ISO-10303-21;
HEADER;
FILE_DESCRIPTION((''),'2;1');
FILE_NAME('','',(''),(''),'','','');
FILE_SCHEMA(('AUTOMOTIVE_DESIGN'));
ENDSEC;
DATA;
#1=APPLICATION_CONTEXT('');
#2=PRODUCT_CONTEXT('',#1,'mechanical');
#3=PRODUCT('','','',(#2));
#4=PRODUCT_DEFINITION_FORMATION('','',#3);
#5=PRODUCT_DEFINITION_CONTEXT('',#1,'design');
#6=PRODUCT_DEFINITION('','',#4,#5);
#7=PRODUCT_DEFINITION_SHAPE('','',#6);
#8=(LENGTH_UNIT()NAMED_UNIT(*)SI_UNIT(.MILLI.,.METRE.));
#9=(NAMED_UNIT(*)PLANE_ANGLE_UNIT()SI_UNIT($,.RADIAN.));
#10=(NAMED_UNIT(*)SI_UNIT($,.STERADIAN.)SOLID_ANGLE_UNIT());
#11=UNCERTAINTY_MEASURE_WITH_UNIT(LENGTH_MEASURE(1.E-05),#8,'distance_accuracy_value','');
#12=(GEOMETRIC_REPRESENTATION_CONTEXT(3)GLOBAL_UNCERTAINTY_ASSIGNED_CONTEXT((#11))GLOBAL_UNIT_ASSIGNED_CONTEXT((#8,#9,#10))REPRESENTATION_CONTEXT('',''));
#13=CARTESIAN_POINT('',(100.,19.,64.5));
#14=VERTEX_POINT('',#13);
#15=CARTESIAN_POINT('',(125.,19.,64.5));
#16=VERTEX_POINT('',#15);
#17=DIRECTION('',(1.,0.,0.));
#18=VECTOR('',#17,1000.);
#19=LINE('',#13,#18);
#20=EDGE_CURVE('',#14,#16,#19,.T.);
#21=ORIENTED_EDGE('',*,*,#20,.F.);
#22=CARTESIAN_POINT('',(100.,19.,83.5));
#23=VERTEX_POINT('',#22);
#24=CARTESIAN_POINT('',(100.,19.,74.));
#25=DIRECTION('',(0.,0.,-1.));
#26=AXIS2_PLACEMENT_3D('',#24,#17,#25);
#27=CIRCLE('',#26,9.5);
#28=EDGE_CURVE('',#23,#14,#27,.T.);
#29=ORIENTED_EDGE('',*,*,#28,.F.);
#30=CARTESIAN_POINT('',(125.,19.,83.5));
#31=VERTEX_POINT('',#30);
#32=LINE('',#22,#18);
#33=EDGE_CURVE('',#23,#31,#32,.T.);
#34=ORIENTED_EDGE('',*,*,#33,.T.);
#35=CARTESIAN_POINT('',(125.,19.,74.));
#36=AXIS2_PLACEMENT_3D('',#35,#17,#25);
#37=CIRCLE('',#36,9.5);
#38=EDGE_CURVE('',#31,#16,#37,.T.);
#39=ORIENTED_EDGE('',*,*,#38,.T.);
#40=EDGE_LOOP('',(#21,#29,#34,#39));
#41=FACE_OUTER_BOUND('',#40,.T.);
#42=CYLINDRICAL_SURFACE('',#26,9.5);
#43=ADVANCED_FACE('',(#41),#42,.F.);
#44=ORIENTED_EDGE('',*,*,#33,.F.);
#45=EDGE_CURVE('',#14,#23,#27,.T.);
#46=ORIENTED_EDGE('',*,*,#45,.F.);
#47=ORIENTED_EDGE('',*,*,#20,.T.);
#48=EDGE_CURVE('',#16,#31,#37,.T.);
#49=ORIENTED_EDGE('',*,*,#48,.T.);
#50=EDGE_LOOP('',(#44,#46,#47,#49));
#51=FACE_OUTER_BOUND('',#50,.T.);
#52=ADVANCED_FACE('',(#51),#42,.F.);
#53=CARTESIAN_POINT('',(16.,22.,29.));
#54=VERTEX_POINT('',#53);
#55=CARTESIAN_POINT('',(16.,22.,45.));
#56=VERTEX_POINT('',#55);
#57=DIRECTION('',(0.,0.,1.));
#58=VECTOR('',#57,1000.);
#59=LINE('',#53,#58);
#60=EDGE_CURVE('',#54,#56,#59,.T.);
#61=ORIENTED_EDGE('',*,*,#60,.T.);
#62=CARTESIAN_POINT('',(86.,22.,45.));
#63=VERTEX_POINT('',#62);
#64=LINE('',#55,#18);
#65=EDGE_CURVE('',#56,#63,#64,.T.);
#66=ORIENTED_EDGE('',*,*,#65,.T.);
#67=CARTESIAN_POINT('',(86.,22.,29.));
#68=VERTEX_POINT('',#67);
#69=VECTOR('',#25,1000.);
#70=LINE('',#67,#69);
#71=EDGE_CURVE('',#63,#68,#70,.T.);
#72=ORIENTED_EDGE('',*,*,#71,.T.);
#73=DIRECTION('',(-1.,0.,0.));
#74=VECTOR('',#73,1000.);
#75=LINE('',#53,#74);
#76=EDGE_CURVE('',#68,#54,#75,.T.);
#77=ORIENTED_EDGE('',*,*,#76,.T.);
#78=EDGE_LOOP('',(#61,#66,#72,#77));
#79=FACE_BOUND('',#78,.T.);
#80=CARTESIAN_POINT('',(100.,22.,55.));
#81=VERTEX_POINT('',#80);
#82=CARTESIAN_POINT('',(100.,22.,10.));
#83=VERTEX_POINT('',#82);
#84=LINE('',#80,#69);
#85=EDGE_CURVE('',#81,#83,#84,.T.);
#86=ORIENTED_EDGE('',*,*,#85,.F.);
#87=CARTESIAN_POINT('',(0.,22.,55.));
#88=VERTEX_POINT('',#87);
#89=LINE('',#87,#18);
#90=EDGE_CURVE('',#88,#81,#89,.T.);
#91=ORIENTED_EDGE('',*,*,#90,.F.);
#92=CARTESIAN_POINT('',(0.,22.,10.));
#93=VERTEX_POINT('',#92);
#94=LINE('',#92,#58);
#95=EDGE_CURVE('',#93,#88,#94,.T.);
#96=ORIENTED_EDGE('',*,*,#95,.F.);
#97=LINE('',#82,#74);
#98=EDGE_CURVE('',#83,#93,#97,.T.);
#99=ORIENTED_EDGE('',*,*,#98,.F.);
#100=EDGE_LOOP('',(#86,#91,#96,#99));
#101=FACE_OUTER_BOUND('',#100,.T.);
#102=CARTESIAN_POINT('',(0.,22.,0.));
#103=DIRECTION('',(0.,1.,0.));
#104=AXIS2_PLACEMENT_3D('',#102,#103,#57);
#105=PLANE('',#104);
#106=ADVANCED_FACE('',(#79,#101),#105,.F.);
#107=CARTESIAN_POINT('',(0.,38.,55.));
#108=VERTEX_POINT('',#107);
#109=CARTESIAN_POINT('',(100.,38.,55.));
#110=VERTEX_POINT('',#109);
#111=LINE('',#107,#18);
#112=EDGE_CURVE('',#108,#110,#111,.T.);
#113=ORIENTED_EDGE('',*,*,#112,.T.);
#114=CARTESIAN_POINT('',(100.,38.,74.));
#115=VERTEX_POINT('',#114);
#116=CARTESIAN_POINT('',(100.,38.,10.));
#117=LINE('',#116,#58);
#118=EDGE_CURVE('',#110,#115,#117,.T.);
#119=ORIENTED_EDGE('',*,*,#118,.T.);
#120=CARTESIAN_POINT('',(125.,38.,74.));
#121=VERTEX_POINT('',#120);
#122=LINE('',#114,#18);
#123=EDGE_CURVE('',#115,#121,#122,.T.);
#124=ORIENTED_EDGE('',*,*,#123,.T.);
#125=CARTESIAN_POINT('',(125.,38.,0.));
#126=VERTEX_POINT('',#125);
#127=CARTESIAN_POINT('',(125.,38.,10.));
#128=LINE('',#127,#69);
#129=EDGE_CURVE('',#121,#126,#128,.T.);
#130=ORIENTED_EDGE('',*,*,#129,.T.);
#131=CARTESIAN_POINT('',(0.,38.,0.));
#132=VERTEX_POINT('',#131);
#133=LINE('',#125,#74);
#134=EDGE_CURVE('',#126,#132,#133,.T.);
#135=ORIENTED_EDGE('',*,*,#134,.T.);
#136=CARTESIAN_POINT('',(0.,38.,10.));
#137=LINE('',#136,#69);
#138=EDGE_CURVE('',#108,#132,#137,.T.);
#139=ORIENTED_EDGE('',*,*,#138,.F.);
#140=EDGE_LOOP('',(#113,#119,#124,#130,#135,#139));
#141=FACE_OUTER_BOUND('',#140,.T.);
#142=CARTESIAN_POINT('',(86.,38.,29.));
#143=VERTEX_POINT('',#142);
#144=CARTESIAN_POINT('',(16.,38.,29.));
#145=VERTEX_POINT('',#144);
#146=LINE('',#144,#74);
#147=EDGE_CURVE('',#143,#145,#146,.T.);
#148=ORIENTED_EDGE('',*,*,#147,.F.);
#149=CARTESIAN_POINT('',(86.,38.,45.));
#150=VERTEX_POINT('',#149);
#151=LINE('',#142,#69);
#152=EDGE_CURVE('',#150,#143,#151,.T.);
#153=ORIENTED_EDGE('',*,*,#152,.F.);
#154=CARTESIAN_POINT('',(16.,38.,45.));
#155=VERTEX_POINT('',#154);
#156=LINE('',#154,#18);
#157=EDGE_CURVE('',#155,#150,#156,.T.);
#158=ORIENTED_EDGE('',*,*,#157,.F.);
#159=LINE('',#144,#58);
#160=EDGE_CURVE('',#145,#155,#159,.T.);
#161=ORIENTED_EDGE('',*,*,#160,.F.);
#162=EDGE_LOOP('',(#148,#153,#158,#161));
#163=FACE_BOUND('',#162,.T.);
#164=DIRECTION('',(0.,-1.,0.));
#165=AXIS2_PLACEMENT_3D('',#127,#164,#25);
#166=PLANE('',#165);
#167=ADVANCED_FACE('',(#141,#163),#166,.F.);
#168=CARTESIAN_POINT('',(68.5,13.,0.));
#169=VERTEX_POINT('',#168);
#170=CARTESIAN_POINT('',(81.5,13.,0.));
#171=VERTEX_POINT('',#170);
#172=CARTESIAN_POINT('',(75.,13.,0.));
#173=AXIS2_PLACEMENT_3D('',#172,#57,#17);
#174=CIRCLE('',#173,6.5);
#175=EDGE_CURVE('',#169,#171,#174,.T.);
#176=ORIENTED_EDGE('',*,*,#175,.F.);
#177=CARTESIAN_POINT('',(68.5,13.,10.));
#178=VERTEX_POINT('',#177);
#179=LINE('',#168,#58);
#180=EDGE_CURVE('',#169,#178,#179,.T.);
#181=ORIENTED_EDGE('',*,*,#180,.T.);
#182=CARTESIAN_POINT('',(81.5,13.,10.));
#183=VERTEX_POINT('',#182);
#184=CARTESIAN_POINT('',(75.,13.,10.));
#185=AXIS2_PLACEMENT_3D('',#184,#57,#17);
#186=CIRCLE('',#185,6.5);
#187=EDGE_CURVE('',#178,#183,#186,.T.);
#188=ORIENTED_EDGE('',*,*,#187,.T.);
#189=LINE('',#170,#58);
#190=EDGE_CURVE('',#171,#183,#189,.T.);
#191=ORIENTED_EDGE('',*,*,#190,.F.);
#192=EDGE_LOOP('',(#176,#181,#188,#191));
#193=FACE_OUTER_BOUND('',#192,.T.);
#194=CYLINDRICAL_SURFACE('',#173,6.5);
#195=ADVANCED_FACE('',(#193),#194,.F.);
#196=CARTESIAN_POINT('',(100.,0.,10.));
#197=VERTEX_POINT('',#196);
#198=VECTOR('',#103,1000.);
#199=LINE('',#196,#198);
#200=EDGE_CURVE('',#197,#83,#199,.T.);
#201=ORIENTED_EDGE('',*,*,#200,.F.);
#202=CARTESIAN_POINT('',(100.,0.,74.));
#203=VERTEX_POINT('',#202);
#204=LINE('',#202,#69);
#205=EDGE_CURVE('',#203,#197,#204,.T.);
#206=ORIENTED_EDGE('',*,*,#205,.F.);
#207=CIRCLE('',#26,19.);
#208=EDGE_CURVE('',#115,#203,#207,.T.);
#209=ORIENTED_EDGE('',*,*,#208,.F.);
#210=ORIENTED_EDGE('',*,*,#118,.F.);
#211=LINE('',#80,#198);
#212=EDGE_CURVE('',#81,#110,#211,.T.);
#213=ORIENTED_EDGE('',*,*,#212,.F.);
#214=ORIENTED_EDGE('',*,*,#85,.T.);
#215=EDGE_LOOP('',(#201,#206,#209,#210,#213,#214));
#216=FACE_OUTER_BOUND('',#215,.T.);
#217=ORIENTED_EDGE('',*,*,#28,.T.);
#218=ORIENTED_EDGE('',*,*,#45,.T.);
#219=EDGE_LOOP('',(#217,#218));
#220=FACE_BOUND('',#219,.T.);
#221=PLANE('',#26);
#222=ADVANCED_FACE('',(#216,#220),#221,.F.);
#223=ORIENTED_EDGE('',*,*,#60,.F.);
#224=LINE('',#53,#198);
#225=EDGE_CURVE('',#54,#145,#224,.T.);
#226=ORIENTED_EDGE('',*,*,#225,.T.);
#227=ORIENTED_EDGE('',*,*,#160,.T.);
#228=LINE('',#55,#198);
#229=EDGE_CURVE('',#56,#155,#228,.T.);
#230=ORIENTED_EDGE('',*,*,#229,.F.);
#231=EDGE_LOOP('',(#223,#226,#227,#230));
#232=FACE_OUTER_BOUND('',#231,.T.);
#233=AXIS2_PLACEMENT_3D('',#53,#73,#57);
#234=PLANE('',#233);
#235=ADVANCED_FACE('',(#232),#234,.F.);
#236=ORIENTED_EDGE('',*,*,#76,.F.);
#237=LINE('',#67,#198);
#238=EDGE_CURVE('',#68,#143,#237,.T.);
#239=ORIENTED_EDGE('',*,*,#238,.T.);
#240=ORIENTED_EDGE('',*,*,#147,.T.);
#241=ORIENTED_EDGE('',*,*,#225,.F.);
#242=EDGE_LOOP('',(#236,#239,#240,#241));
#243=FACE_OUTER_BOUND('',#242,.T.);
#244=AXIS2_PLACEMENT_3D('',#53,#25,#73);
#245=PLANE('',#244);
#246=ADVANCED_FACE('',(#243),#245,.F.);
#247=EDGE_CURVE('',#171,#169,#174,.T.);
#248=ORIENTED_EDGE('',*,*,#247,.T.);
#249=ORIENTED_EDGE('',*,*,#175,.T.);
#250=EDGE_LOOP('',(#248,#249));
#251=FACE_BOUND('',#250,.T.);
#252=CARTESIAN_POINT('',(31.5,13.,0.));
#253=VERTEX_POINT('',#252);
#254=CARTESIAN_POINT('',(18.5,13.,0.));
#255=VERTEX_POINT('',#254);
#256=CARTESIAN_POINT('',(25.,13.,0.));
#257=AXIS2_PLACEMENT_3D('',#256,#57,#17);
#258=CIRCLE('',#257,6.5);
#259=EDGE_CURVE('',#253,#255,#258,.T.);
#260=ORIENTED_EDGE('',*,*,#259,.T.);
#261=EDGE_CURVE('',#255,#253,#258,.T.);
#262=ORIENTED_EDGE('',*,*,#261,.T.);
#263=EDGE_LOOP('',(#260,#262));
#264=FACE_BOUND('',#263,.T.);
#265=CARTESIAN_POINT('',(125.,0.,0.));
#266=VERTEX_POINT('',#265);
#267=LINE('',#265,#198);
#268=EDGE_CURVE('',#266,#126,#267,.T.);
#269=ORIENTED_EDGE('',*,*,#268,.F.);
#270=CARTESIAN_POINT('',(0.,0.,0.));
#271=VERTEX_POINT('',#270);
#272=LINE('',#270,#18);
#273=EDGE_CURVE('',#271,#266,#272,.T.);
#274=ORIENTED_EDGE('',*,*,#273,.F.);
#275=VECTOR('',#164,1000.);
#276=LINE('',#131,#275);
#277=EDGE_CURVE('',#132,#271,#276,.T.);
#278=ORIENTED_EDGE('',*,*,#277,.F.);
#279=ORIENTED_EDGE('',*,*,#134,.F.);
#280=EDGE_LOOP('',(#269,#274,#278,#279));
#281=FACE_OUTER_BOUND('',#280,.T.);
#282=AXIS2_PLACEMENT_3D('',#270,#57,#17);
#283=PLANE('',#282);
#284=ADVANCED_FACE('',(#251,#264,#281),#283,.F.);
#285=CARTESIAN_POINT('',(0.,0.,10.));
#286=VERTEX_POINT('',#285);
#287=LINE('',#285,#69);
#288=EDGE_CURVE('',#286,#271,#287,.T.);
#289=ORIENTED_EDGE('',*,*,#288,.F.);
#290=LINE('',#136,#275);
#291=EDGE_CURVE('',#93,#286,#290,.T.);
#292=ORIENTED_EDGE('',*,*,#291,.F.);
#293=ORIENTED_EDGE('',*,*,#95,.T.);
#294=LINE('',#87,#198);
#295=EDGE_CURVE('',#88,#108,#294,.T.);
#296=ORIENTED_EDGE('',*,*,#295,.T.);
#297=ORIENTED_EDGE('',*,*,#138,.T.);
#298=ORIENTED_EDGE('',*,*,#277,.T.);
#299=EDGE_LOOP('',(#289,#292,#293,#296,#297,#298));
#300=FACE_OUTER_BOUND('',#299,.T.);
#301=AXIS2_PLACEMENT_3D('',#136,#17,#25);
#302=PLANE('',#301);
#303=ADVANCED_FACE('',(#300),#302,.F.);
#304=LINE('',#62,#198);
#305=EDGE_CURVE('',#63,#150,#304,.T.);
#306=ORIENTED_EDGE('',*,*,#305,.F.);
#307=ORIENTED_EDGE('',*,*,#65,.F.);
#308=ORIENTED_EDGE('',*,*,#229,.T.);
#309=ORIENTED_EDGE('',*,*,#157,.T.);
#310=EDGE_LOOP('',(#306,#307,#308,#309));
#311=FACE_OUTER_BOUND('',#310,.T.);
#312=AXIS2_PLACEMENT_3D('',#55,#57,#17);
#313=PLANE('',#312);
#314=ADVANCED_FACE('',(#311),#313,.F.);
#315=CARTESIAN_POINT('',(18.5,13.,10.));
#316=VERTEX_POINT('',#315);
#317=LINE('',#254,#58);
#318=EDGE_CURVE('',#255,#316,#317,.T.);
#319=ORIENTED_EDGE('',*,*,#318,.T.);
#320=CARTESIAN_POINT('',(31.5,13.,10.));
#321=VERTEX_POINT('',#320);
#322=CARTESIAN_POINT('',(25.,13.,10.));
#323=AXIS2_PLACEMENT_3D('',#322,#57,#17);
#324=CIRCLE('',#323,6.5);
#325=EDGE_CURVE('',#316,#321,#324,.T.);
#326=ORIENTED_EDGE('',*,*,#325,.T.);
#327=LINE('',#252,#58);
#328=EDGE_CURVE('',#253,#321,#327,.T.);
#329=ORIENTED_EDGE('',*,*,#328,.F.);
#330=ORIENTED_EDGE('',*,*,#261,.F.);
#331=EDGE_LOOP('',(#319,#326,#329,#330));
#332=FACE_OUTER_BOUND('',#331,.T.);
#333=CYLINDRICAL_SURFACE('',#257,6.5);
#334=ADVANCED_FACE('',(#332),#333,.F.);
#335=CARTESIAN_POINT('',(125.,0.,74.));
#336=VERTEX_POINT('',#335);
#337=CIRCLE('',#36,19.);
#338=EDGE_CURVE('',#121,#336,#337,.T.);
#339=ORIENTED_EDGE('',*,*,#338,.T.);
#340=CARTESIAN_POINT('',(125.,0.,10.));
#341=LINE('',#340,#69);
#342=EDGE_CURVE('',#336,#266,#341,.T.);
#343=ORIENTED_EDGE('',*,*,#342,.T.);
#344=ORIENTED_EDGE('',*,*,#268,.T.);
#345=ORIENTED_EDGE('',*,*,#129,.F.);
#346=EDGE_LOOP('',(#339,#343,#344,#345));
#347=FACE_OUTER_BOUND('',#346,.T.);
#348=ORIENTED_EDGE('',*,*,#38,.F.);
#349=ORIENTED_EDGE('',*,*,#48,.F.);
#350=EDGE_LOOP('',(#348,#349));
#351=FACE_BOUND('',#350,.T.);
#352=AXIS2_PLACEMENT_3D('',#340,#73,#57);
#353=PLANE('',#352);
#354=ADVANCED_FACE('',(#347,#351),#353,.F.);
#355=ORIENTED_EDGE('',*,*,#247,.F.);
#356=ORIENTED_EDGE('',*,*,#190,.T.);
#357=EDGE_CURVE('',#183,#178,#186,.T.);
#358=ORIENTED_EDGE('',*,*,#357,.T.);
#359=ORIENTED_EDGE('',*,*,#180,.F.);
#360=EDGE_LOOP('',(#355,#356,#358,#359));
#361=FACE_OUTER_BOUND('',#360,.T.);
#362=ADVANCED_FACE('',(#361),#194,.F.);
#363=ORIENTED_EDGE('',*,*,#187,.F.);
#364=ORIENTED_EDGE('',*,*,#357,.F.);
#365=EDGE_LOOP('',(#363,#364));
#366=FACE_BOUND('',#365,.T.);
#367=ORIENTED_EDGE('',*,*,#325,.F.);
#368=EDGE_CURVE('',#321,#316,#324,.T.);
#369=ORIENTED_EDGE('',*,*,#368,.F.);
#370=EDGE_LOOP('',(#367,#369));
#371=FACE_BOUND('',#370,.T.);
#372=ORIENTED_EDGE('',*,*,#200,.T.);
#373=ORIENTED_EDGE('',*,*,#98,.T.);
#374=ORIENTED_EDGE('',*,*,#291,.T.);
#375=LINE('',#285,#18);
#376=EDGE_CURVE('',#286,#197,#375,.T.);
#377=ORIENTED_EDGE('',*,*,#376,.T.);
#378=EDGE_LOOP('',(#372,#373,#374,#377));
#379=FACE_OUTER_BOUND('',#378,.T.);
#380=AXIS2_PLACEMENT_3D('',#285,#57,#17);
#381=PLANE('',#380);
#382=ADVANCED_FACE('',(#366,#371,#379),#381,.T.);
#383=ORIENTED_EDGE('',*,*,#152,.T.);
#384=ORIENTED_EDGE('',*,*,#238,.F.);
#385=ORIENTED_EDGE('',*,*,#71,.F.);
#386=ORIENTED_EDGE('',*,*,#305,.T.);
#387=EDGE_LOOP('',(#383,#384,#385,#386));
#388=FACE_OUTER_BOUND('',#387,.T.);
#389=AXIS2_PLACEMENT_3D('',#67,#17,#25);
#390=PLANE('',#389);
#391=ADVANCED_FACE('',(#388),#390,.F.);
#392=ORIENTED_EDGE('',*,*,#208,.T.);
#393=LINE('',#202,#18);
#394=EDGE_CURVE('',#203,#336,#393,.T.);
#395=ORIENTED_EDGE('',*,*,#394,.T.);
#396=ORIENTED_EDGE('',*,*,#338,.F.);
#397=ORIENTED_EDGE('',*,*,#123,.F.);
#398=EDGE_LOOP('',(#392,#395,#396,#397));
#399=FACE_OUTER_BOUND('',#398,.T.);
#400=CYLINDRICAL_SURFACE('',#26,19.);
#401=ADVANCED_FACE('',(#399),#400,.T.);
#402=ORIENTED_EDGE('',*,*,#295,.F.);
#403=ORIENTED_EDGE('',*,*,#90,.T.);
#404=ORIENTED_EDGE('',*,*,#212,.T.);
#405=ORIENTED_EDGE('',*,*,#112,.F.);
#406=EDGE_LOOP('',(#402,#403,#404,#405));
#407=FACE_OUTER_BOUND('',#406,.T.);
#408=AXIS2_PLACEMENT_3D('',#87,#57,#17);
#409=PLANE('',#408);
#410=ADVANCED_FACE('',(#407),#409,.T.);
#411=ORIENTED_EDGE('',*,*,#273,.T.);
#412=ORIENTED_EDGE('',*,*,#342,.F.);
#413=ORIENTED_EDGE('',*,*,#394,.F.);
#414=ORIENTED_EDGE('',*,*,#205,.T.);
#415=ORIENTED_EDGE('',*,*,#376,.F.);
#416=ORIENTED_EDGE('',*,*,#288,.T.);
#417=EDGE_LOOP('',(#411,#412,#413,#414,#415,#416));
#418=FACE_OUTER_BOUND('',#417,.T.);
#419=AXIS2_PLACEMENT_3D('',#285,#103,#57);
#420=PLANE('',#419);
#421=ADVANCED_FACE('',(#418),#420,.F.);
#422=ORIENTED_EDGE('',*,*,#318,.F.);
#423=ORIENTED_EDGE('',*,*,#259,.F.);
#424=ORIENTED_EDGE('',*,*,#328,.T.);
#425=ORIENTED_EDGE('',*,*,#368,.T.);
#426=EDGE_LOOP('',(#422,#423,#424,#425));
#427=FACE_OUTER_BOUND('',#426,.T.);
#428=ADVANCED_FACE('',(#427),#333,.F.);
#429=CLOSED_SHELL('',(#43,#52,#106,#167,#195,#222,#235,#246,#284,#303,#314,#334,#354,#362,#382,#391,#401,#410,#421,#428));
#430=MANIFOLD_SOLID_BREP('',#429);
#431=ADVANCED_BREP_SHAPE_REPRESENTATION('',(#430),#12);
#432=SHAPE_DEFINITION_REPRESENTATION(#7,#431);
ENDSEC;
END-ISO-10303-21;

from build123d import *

# Parameters (mm, degrees)
BASE_PLATE_SKETCH_W   = 125
BASE_PLATE_SKETCH_H   = 38
BASE_PLATE_DEPTH      = 10
HINGE_LUG_DEPTH       = 25
LUG_BORE_19_SKETCH_R  = 9.5
LUG_BORE_19_DEPTH     = 25
ARM_SKETCH_W          = 100
ARM_SKETCH_H          = 45
ARM_DEPTH             = 16
SLOT_70X16_SKETCH_W   = 70
SLOT_70X16_SKETCH_H   = 16
SLOT_70X16_DEPTH      = 16
CORNER_NOTCH_SKETCH_R = 6.5
CORNER_NOTCH_DEPTH    = 10


with BuildPart() as part:
    # Base Plate Sketch → Base Plate (new body)
    with BuildSketch(Plane.XY):
        with Locations((62.5, 19)):
            Rectangle(BASE_PLATE_SKETCH_W, BASE_PLATE_SKETCH_H)
    extrude(amount=BASE_PLATE_DEPTH)

    # Hinge Lug Sketch → Hinge Lug (add)
    with BuildSketch(Plane(origin=(125, 0, 0), x_dir=(0, 0, -1), z_dir=(1, 0, 0))):
        with BuildLine():
            Line((-10, 38), (-74, 38))
            ThreePointArc((-74, 38), (-93, 19), (-74, 0))
            Line((-74, 0), (-10, 0))
            Line((-10, 0), (-10, 38))
        make_face()
    extrude(amount=-HINGE_LUG_DEPTH)

    # Lug Bore Ø19 Sketch → Lug Bore Ø19 (cut)
    with BuildSketch(Plane(origin=(125, 0, 0), x_dir=(0, 0, -1), z_dir=(1, 0, 0))):
        with Locations((-74, 19)):
            Circle(LUG_BORE_19_SKETCH_R)
    extrude(amount=-LUG_BORE_19_DEPTH, mode=Mode.SUBTRACT)

    # Arm Sketch → Arm (add)
    with BuildSketch(Plane(origin=(0, 38, 0), x_dir=(1, 0, 0), z_dir=(0, 1, 0))):
        with Locations((50, -32.5)):
            Rectangle(ARM_SKETCH_W, ARM_SKETCH_H)
    extrude(amount=-ARM_DEPTH)

    # Slot 70x16 Sketch → Slot 70x16 (cut)
    with BuildSketch(Plane(origin=(0, 38, 0), x_dir=(1, 0, 0), z_dir=(0, 1, 0))):
        with Locations((51, -37)):
            Rectangle(SLOT_70X16_SKETCH_W, SLOT_70X16_SKETCH_H)
    extrude(amount=-SLOT_70X16_DEPTH, mode=Mode.SUBTRACT)

    # Corner Notch Sketch → Corner Notch (cut)
    with BuildSketch(Plane.XY.offset(10)):
        with Locations((25, 13)):
            Circle(CORNER_NOTCH_SKETCH_R)
        with Locations((75, 13)):
            Circle(CORNER_NOTCH_SKETCH_R)
    extrude(amount=-CORNER_NOTCH_DEPTH, mode=Mode.SUBTRACT)


solid = part.part
